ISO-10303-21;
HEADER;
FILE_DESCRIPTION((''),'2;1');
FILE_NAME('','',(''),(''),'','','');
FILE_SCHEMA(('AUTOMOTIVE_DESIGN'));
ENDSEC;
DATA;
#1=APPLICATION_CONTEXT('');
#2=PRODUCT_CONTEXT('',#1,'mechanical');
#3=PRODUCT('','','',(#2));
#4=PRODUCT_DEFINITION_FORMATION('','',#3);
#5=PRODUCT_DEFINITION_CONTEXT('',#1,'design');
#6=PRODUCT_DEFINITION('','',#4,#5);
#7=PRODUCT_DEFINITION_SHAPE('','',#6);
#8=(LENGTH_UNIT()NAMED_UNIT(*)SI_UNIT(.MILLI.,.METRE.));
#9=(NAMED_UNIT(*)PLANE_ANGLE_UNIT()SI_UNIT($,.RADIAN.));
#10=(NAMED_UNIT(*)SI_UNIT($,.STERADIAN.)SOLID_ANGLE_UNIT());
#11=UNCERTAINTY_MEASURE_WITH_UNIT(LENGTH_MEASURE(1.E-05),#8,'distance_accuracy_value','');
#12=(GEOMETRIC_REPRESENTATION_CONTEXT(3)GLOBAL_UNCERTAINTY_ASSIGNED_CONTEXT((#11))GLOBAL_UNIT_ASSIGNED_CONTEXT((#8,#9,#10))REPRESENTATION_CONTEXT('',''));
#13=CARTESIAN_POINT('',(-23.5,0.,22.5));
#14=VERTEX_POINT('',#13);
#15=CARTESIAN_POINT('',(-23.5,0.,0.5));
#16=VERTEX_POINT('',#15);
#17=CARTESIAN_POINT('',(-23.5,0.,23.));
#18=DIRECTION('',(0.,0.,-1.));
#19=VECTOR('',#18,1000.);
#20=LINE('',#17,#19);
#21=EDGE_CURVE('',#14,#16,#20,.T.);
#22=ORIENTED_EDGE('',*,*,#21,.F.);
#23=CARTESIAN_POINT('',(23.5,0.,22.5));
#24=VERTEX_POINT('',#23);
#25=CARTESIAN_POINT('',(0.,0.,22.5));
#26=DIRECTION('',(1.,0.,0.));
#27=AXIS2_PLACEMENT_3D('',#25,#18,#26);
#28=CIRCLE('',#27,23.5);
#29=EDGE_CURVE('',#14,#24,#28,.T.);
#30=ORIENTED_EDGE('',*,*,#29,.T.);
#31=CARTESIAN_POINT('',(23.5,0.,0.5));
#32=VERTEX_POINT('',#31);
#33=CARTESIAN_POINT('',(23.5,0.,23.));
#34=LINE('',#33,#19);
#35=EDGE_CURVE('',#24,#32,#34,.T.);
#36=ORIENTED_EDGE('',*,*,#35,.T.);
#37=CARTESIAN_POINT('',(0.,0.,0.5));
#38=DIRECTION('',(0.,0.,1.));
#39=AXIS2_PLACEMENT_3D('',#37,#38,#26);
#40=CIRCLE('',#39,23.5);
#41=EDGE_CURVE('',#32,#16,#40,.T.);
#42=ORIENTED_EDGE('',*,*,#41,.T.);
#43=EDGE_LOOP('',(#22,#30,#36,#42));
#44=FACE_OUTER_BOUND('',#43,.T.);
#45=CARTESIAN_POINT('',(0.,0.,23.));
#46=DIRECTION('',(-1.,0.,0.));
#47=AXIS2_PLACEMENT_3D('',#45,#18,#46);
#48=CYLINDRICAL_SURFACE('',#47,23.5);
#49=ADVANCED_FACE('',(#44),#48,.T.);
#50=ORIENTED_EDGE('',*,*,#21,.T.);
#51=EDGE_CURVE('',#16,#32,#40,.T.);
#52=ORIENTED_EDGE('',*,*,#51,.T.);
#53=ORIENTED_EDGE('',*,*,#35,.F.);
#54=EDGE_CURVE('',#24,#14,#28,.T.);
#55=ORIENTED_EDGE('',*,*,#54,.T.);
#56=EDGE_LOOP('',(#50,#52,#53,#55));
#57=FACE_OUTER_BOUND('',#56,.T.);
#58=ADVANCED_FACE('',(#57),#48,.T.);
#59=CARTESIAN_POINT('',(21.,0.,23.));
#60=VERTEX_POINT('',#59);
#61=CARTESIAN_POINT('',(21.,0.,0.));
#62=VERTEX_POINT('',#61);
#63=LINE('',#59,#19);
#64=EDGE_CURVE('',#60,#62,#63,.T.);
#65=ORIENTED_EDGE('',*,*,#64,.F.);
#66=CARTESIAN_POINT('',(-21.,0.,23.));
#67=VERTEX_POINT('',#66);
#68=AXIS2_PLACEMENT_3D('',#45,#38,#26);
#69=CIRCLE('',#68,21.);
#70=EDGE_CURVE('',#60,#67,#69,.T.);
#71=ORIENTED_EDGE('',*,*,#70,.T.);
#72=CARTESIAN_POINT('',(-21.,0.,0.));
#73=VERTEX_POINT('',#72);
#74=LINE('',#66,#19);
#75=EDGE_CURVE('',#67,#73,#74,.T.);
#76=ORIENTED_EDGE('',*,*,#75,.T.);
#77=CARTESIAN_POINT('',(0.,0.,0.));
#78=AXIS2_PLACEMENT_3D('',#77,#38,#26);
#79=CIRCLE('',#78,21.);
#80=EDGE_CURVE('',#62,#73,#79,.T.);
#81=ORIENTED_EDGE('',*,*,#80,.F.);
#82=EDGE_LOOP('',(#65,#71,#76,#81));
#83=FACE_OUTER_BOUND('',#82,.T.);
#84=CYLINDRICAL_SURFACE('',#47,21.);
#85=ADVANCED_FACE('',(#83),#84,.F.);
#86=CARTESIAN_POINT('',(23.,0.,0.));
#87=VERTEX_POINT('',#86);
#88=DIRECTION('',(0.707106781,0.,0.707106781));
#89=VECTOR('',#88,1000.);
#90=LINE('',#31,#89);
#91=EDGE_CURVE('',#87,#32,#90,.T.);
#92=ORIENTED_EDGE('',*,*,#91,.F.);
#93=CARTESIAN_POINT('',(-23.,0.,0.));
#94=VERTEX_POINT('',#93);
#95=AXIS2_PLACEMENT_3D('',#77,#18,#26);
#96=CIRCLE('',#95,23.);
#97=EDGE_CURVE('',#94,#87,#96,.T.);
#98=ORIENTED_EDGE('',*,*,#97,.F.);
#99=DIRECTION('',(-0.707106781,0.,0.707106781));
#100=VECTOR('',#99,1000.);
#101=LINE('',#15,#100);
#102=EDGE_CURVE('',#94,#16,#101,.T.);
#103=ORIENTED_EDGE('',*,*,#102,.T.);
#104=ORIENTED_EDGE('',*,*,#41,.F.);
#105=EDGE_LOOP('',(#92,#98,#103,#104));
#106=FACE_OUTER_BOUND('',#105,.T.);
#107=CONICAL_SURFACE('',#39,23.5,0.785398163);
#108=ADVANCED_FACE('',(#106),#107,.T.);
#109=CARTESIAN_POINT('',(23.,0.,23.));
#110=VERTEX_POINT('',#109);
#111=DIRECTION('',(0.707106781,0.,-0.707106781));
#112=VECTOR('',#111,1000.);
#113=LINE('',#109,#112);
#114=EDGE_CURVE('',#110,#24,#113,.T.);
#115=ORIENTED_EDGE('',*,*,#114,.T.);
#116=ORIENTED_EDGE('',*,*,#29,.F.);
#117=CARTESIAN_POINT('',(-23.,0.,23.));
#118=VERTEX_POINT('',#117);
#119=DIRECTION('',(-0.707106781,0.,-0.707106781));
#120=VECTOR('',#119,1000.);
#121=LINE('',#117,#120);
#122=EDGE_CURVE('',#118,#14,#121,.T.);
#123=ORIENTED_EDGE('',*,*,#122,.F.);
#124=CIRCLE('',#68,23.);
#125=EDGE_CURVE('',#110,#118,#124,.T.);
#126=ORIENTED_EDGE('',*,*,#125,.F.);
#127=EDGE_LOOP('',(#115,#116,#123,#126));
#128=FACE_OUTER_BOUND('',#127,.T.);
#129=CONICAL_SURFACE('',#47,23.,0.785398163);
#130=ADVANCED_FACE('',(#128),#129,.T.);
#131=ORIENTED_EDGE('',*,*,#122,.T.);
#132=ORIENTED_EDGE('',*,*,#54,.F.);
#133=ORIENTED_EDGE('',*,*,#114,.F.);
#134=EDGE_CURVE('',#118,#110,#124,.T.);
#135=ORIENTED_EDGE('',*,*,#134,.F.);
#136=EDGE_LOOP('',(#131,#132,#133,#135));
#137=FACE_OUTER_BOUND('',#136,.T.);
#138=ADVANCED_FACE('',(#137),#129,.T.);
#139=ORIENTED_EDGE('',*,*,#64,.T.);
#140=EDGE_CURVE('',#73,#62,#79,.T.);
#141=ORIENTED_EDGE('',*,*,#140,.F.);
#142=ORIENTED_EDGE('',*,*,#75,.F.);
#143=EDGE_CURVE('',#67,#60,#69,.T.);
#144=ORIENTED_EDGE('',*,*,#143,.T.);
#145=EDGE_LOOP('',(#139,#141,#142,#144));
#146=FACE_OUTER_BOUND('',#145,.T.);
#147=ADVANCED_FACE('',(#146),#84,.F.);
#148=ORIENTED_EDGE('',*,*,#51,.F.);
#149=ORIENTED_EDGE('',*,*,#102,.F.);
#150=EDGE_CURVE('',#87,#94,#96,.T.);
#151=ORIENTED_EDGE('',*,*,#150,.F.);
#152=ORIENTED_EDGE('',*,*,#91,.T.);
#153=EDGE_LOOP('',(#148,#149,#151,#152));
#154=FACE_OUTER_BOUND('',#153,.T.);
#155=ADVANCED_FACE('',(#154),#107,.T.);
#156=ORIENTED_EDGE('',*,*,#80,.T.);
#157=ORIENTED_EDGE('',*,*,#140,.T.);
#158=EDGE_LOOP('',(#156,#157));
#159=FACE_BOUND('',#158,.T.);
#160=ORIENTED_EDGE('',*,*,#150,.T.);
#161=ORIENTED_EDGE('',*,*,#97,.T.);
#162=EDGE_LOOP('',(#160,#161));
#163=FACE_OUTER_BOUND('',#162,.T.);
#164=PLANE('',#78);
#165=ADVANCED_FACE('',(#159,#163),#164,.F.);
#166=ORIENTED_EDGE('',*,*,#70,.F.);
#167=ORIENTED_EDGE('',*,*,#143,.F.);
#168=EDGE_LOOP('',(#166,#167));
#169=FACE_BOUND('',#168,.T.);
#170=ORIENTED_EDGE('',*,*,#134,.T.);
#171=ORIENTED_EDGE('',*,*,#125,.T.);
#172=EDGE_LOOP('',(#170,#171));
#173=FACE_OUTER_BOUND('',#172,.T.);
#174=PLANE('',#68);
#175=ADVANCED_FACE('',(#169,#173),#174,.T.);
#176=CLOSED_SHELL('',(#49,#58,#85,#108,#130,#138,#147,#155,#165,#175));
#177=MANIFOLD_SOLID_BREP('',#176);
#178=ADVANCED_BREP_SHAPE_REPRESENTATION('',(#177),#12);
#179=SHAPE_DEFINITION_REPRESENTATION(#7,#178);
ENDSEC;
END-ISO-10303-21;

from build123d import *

# Parameters (mm, degrees)
SKETCH1_R           = 23.5
SKETCH1_R_2         = 21
BOSS_EXTRUDE1_DEPTH = 23
CHAMFER1_SIZE       = 0.5


with BuildPart() as part:
    # Sketch1 → Boss-Extrude1 (new body)
    with BuildSketch(Plane.XY):
        Circle(SKETCH1_R)
        Circle(SKETCH1_R_2, mode=Mode.SUBTRACT)
    extrude(amount=BOSS_EXTRUDE1_DEPTH)

    # Chamfer1
    chamfer1_edges = [part.edges().sort_by_distance(p)[0] for p in [
        (-23.5, 0, 0),
        (-23.5, 0, 23),
    ]]
    chamfer(chamfer1_edges, length=CHAMFER1_SIZE)


solid = part.part
